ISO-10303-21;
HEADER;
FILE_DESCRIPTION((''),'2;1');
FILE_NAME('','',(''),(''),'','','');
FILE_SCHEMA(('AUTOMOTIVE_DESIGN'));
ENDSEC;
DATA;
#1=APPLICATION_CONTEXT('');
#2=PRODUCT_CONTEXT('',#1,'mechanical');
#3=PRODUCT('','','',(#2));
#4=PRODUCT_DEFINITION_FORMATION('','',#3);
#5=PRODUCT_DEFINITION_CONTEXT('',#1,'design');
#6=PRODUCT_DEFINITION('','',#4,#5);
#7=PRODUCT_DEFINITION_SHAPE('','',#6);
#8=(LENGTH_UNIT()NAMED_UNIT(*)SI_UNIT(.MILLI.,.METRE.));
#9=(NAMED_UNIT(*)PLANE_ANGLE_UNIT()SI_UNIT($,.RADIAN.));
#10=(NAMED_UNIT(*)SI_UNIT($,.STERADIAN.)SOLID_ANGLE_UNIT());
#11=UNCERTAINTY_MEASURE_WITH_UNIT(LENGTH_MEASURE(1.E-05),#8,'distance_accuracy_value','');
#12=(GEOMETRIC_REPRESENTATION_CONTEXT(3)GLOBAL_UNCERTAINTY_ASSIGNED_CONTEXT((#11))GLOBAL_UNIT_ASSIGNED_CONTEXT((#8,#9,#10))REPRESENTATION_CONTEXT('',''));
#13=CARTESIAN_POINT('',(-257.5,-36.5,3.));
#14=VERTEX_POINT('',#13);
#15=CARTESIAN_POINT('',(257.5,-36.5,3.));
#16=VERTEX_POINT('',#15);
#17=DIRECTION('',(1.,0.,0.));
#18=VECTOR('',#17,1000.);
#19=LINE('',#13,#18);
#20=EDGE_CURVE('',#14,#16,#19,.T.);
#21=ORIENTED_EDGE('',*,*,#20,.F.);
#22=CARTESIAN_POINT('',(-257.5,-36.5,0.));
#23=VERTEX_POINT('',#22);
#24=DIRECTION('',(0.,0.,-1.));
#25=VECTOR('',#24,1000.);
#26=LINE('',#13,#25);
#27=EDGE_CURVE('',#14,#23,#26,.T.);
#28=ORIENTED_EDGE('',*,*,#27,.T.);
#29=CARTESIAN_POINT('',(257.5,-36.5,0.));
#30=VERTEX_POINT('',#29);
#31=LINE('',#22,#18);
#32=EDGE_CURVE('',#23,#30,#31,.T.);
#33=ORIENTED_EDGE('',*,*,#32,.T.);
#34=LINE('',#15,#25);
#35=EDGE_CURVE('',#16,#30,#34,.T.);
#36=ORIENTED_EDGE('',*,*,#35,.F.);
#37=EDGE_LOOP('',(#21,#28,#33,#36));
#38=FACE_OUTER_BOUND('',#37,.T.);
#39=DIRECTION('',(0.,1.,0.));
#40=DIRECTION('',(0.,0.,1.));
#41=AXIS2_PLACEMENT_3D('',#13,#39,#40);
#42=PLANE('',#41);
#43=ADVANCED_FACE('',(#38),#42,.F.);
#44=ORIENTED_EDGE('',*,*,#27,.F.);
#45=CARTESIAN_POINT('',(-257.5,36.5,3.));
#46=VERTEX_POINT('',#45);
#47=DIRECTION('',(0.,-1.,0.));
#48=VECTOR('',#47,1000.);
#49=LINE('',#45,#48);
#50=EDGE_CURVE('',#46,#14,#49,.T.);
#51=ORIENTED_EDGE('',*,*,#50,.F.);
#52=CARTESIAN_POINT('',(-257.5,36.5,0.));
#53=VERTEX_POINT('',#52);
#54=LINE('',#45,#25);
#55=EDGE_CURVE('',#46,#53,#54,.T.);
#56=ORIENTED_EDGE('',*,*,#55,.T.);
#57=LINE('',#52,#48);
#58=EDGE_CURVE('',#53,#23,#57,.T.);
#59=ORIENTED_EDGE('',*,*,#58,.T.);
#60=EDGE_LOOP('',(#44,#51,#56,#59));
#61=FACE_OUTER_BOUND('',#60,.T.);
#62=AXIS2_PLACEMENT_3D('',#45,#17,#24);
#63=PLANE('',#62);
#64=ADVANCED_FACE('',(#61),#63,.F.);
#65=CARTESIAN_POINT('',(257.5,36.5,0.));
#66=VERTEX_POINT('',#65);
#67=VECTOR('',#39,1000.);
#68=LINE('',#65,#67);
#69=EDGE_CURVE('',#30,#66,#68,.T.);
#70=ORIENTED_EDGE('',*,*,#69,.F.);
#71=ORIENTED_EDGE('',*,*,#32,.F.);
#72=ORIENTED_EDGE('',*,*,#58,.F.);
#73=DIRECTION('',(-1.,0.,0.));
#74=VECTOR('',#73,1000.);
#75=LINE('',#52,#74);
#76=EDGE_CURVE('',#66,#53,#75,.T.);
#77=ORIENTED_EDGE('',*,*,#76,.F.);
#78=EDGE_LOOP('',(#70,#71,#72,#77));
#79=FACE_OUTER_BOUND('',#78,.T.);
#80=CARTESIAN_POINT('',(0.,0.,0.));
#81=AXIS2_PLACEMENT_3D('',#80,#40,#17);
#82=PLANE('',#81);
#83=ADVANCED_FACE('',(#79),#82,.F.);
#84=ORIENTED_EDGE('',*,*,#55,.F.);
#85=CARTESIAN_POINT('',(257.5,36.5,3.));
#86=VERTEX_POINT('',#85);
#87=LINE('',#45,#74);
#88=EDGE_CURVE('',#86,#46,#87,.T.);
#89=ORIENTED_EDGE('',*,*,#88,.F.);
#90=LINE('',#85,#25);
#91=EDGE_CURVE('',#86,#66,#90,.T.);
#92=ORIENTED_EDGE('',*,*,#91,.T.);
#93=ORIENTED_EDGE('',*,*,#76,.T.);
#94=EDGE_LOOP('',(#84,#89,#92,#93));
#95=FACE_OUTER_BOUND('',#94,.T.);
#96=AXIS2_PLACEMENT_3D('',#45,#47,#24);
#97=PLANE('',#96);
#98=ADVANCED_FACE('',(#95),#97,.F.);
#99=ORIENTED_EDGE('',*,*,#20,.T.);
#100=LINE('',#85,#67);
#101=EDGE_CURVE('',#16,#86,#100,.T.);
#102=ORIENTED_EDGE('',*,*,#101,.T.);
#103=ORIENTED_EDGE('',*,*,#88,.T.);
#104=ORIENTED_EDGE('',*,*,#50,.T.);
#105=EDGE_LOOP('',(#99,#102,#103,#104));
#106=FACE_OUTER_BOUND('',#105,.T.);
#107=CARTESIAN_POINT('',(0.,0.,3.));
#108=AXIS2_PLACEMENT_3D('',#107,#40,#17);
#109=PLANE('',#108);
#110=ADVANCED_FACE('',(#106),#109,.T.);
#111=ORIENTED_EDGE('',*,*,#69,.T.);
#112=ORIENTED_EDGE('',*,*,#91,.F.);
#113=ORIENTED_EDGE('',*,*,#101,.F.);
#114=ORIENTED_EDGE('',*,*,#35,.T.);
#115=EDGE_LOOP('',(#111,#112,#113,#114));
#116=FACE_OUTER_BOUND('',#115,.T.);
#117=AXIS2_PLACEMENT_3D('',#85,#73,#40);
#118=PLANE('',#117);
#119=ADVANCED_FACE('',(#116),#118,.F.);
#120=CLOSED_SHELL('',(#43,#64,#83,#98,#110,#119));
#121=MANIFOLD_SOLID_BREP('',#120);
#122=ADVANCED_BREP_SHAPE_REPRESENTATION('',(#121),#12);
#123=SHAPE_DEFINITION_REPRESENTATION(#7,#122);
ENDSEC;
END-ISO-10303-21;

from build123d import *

# Parameters (mm, degrees)
SKETCH1_W           = 515
SKETCH1_H           = 73
BOSS_EXTRUDE1_DEPTH = 3


with BuildPart() as part:
    # Sketch1 → Boss-Extrude1 (new body)
    with BuildSketch(Plane.XY):
        Rectangle(SKETCH1_W, SKETCH1_H)
    extrude(amount=BOSS_EXTRUDE1_DEPTH)


solid = part.part
